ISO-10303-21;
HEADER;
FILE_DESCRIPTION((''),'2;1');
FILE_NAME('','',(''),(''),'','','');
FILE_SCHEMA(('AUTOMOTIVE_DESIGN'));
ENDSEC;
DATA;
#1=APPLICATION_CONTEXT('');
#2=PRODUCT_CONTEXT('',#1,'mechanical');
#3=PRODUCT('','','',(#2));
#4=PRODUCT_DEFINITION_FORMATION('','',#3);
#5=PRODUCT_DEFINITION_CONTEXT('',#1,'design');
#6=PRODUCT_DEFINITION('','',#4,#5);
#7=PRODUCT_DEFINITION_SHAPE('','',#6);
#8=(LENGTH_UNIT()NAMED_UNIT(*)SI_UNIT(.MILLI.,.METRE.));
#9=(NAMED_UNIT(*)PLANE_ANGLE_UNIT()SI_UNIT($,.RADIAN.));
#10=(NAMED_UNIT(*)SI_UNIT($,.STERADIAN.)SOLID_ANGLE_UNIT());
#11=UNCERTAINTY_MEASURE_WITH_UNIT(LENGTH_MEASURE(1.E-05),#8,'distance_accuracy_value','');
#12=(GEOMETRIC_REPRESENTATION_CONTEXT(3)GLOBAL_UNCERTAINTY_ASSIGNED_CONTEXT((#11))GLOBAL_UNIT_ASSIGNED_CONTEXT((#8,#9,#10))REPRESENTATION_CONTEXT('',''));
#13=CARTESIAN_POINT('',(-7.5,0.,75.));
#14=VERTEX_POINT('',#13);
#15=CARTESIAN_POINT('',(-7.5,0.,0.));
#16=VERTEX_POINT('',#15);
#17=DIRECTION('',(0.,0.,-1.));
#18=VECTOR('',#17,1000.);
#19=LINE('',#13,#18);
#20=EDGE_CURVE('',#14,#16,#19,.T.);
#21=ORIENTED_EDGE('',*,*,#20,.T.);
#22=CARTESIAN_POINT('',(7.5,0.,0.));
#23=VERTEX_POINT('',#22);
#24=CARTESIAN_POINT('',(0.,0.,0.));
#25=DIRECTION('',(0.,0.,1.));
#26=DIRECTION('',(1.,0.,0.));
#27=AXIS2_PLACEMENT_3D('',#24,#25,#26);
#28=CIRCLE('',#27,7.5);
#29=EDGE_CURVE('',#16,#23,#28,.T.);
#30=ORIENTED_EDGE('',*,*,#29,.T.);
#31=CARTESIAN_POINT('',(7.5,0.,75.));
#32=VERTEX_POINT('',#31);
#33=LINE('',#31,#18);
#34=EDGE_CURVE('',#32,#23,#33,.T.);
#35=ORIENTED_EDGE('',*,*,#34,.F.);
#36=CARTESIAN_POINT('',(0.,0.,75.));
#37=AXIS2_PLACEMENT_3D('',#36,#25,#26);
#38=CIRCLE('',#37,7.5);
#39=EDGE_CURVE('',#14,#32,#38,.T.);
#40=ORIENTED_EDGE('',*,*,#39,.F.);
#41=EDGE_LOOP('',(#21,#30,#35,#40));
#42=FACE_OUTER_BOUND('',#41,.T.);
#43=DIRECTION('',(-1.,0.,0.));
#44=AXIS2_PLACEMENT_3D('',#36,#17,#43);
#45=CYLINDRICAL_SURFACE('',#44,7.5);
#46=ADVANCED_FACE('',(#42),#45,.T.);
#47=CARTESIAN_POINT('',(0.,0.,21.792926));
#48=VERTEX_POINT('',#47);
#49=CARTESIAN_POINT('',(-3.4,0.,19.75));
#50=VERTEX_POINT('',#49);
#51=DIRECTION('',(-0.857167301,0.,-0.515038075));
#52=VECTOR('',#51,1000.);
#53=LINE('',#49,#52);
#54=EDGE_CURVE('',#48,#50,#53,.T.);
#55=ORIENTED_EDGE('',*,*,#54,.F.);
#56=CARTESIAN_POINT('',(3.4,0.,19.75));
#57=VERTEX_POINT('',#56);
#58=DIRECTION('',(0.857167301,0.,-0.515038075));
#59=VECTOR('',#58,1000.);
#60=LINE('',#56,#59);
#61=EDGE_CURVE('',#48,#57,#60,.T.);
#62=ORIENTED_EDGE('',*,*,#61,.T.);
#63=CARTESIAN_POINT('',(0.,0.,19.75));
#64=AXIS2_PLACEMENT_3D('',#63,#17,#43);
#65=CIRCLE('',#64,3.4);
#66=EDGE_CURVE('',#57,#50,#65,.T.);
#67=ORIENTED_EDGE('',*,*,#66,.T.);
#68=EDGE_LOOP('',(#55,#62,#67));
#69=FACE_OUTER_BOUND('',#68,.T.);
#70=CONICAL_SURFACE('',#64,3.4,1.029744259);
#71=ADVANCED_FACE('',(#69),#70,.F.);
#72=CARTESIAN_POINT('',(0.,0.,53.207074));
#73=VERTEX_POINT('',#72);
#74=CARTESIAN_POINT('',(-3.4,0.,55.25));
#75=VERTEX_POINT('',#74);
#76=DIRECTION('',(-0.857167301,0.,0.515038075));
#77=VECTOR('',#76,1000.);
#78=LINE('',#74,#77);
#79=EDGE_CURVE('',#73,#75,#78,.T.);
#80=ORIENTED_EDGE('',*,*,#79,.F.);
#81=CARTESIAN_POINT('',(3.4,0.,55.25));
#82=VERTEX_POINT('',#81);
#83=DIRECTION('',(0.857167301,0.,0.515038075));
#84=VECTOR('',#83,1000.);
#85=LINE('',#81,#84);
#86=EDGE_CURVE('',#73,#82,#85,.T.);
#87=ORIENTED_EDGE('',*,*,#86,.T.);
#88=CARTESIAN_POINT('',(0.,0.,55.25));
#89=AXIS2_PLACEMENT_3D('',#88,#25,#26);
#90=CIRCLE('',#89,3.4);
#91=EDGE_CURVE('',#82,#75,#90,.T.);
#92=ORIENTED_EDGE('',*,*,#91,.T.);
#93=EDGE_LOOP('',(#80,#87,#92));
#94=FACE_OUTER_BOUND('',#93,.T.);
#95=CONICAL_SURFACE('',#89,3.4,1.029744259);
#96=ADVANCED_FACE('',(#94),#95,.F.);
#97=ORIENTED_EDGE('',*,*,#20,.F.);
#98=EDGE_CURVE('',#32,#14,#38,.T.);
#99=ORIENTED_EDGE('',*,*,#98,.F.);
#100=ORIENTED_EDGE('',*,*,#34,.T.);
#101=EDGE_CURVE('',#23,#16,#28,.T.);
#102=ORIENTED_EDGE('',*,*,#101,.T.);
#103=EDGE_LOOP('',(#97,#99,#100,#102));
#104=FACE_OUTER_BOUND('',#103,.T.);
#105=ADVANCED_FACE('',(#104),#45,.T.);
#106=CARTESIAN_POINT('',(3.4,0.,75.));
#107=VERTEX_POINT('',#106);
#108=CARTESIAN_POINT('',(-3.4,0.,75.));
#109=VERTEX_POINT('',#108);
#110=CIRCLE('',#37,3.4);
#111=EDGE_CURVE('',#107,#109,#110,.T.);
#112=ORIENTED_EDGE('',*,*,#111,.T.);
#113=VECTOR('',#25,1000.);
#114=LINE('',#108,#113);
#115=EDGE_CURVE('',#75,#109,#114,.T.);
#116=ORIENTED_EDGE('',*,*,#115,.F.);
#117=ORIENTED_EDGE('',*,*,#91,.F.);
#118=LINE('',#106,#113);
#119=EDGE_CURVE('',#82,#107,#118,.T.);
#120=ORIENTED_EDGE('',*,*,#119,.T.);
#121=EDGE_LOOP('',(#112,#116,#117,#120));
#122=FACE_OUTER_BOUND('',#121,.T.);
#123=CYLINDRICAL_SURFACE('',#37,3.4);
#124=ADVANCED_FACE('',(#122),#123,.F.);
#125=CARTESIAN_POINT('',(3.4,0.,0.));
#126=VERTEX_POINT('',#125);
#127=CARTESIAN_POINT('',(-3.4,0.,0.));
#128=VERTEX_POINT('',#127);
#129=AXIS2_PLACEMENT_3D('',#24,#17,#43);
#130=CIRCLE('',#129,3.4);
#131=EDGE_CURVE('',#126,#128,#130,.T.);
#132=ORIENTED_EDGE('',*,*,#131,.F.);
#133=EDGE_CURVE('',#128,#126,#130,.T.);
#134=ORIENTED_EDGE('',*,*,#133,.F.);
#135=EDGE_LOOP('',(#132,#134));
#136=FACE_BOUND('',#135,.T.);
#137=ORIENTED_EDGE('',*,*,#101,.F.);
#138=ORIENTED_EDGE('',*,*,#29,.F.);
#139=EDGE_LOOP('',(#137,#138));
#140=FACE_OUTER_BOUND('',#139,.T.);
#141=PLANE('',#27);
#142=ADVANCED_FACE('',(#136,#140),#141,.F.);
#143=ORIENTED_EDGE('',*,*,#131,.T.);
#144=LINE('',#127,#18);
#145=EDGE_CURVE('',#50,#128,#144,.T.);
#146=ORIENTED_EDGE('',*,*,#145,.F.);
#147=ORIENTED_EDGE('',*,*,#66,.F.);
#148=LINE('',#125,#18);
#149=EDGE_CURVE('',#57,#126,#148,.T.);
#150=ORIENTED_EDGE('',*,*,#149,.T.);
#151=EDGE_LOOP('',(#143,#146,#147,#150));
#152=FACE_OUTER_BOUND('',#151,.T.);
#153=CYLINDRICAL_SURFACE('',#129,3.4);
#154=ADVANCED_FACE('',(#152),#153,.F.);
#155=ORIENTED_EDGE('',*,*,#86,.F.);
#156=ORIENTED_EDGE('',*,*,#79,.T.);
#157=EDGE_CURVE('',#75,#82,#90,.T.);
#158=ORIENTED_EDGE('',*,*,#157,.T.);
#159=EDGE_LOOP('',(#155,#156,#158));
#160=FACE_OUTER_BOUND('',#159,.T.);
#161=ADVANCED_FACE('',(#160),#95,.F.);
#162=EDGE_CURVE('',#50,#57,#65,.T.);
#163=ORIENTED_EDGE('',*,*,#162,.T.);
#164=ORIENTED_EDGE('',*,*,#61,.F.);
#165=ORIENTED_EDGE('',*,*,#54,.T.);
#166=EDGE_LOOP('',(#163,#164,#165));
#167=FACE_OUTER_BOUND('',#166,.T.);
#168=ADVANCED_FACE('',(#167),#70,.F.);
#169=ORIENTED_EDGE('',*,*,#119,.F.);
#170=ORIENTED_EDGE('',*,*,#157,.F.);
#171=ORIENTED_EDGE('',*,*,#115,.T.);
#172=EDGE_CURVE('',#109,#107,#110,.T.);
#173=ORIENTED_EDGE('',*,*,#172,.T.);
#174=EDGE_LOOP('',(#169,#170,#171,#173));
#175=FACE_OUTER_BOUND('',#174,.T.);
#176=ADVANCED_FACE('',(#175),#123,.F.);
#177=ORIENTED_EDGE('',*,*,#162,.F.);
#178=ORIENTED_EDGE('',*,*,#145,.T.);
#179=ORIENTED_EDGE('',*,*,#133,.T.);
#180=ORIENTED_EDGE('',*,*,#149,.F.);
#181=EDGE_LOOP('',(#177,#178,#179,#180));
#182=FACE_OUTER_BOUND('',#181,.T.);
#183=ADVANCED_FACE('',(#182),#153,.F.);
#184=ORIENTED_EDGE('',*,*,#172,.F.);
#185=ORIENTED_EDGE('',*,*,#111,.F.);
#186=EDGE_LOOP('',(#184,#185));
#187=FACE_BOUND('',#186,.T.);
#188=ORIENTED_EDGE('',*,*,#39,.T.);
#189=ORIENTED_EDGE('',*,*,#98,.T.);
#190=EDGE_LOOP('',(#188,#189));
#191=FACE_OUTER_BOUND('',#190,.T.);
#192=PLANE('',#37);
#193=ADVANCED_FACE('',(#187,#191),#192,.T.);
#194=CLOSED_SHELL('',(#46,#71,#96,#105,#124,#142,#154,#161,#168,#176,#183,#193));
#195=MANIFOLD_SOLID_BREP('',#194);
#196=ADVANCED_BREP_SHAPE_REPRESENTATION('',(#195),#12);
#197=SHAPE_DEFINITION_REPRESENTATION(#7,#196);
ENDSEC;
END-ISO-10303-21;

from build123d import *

# Parameters (mm, degrees)
SKETCH1_R             = 7.5
BOSS_EXTRUDE1_DEPTH   = 75
M8_TAPPED_HOLE1_D     = 6.8
M8_TAPPED_HOLE1_DEPTH = 19.75
M8_TAPPED_HOLE1_TIP   = 2.042926105
M8_TAPPED_HOLE2_D     = 6.8
M8_TAPPED_HOLE2_DEPTH = 19.75
M8_TAPPED_HOLE2_TIP   = 2.042926105


with BuildPart() as part:
    # Sketch1 → Boss-Extrude1 (new body)
    with BuildSketch(Plane.XY):
        Circle(SKETCH1_R)
    extrude(amount=BOSS_EXTRUDE1_DEPTH)

    # M8 Tapped Hole1
    with Locations(Plane.XY.offset(75)):
        with Locations((0, 0)):
            Hole(M8_TAPPED_HOLE1_D / 2, depth=M8_TAPPED_HOLE1_DEPTH)
            with Locations((0, 0, -(M8_TAPPED_HOLE1_DEPTH + M8_TAPPED_HOLE1_TIP / 2))):  # 118° drill point
                Cone(0, M8_TAPPED_HOLE1_D / 2, M8_TAPPED_HOLE1_TIP, mode=Mode.SUBTRACT)

    # M8 Tapped Hole2
    with Locations(Plane(origin=(0, 0, 0), x_dir=(-1, 0, 0), z_dir=(0, 0, -1))):
        with Locations((0, 0)):
            Hole(M8_TAPPED_HOLE2_D / 2, depth=M8_TAPPED_HOLE2_DEPTH)
            with Locations((0, 0, -(M8_TAPPED_HOLE2_DEPTH + M8_TAPPED_HOLE2_TIP / 2))):  # 118° drill point
                Cone(0, M8_TAPPED_HOLE2_D / 2, M8_TAPPED_HOLE2_TIP, mode=Mode.SUBTRACT)


solid = part.part
